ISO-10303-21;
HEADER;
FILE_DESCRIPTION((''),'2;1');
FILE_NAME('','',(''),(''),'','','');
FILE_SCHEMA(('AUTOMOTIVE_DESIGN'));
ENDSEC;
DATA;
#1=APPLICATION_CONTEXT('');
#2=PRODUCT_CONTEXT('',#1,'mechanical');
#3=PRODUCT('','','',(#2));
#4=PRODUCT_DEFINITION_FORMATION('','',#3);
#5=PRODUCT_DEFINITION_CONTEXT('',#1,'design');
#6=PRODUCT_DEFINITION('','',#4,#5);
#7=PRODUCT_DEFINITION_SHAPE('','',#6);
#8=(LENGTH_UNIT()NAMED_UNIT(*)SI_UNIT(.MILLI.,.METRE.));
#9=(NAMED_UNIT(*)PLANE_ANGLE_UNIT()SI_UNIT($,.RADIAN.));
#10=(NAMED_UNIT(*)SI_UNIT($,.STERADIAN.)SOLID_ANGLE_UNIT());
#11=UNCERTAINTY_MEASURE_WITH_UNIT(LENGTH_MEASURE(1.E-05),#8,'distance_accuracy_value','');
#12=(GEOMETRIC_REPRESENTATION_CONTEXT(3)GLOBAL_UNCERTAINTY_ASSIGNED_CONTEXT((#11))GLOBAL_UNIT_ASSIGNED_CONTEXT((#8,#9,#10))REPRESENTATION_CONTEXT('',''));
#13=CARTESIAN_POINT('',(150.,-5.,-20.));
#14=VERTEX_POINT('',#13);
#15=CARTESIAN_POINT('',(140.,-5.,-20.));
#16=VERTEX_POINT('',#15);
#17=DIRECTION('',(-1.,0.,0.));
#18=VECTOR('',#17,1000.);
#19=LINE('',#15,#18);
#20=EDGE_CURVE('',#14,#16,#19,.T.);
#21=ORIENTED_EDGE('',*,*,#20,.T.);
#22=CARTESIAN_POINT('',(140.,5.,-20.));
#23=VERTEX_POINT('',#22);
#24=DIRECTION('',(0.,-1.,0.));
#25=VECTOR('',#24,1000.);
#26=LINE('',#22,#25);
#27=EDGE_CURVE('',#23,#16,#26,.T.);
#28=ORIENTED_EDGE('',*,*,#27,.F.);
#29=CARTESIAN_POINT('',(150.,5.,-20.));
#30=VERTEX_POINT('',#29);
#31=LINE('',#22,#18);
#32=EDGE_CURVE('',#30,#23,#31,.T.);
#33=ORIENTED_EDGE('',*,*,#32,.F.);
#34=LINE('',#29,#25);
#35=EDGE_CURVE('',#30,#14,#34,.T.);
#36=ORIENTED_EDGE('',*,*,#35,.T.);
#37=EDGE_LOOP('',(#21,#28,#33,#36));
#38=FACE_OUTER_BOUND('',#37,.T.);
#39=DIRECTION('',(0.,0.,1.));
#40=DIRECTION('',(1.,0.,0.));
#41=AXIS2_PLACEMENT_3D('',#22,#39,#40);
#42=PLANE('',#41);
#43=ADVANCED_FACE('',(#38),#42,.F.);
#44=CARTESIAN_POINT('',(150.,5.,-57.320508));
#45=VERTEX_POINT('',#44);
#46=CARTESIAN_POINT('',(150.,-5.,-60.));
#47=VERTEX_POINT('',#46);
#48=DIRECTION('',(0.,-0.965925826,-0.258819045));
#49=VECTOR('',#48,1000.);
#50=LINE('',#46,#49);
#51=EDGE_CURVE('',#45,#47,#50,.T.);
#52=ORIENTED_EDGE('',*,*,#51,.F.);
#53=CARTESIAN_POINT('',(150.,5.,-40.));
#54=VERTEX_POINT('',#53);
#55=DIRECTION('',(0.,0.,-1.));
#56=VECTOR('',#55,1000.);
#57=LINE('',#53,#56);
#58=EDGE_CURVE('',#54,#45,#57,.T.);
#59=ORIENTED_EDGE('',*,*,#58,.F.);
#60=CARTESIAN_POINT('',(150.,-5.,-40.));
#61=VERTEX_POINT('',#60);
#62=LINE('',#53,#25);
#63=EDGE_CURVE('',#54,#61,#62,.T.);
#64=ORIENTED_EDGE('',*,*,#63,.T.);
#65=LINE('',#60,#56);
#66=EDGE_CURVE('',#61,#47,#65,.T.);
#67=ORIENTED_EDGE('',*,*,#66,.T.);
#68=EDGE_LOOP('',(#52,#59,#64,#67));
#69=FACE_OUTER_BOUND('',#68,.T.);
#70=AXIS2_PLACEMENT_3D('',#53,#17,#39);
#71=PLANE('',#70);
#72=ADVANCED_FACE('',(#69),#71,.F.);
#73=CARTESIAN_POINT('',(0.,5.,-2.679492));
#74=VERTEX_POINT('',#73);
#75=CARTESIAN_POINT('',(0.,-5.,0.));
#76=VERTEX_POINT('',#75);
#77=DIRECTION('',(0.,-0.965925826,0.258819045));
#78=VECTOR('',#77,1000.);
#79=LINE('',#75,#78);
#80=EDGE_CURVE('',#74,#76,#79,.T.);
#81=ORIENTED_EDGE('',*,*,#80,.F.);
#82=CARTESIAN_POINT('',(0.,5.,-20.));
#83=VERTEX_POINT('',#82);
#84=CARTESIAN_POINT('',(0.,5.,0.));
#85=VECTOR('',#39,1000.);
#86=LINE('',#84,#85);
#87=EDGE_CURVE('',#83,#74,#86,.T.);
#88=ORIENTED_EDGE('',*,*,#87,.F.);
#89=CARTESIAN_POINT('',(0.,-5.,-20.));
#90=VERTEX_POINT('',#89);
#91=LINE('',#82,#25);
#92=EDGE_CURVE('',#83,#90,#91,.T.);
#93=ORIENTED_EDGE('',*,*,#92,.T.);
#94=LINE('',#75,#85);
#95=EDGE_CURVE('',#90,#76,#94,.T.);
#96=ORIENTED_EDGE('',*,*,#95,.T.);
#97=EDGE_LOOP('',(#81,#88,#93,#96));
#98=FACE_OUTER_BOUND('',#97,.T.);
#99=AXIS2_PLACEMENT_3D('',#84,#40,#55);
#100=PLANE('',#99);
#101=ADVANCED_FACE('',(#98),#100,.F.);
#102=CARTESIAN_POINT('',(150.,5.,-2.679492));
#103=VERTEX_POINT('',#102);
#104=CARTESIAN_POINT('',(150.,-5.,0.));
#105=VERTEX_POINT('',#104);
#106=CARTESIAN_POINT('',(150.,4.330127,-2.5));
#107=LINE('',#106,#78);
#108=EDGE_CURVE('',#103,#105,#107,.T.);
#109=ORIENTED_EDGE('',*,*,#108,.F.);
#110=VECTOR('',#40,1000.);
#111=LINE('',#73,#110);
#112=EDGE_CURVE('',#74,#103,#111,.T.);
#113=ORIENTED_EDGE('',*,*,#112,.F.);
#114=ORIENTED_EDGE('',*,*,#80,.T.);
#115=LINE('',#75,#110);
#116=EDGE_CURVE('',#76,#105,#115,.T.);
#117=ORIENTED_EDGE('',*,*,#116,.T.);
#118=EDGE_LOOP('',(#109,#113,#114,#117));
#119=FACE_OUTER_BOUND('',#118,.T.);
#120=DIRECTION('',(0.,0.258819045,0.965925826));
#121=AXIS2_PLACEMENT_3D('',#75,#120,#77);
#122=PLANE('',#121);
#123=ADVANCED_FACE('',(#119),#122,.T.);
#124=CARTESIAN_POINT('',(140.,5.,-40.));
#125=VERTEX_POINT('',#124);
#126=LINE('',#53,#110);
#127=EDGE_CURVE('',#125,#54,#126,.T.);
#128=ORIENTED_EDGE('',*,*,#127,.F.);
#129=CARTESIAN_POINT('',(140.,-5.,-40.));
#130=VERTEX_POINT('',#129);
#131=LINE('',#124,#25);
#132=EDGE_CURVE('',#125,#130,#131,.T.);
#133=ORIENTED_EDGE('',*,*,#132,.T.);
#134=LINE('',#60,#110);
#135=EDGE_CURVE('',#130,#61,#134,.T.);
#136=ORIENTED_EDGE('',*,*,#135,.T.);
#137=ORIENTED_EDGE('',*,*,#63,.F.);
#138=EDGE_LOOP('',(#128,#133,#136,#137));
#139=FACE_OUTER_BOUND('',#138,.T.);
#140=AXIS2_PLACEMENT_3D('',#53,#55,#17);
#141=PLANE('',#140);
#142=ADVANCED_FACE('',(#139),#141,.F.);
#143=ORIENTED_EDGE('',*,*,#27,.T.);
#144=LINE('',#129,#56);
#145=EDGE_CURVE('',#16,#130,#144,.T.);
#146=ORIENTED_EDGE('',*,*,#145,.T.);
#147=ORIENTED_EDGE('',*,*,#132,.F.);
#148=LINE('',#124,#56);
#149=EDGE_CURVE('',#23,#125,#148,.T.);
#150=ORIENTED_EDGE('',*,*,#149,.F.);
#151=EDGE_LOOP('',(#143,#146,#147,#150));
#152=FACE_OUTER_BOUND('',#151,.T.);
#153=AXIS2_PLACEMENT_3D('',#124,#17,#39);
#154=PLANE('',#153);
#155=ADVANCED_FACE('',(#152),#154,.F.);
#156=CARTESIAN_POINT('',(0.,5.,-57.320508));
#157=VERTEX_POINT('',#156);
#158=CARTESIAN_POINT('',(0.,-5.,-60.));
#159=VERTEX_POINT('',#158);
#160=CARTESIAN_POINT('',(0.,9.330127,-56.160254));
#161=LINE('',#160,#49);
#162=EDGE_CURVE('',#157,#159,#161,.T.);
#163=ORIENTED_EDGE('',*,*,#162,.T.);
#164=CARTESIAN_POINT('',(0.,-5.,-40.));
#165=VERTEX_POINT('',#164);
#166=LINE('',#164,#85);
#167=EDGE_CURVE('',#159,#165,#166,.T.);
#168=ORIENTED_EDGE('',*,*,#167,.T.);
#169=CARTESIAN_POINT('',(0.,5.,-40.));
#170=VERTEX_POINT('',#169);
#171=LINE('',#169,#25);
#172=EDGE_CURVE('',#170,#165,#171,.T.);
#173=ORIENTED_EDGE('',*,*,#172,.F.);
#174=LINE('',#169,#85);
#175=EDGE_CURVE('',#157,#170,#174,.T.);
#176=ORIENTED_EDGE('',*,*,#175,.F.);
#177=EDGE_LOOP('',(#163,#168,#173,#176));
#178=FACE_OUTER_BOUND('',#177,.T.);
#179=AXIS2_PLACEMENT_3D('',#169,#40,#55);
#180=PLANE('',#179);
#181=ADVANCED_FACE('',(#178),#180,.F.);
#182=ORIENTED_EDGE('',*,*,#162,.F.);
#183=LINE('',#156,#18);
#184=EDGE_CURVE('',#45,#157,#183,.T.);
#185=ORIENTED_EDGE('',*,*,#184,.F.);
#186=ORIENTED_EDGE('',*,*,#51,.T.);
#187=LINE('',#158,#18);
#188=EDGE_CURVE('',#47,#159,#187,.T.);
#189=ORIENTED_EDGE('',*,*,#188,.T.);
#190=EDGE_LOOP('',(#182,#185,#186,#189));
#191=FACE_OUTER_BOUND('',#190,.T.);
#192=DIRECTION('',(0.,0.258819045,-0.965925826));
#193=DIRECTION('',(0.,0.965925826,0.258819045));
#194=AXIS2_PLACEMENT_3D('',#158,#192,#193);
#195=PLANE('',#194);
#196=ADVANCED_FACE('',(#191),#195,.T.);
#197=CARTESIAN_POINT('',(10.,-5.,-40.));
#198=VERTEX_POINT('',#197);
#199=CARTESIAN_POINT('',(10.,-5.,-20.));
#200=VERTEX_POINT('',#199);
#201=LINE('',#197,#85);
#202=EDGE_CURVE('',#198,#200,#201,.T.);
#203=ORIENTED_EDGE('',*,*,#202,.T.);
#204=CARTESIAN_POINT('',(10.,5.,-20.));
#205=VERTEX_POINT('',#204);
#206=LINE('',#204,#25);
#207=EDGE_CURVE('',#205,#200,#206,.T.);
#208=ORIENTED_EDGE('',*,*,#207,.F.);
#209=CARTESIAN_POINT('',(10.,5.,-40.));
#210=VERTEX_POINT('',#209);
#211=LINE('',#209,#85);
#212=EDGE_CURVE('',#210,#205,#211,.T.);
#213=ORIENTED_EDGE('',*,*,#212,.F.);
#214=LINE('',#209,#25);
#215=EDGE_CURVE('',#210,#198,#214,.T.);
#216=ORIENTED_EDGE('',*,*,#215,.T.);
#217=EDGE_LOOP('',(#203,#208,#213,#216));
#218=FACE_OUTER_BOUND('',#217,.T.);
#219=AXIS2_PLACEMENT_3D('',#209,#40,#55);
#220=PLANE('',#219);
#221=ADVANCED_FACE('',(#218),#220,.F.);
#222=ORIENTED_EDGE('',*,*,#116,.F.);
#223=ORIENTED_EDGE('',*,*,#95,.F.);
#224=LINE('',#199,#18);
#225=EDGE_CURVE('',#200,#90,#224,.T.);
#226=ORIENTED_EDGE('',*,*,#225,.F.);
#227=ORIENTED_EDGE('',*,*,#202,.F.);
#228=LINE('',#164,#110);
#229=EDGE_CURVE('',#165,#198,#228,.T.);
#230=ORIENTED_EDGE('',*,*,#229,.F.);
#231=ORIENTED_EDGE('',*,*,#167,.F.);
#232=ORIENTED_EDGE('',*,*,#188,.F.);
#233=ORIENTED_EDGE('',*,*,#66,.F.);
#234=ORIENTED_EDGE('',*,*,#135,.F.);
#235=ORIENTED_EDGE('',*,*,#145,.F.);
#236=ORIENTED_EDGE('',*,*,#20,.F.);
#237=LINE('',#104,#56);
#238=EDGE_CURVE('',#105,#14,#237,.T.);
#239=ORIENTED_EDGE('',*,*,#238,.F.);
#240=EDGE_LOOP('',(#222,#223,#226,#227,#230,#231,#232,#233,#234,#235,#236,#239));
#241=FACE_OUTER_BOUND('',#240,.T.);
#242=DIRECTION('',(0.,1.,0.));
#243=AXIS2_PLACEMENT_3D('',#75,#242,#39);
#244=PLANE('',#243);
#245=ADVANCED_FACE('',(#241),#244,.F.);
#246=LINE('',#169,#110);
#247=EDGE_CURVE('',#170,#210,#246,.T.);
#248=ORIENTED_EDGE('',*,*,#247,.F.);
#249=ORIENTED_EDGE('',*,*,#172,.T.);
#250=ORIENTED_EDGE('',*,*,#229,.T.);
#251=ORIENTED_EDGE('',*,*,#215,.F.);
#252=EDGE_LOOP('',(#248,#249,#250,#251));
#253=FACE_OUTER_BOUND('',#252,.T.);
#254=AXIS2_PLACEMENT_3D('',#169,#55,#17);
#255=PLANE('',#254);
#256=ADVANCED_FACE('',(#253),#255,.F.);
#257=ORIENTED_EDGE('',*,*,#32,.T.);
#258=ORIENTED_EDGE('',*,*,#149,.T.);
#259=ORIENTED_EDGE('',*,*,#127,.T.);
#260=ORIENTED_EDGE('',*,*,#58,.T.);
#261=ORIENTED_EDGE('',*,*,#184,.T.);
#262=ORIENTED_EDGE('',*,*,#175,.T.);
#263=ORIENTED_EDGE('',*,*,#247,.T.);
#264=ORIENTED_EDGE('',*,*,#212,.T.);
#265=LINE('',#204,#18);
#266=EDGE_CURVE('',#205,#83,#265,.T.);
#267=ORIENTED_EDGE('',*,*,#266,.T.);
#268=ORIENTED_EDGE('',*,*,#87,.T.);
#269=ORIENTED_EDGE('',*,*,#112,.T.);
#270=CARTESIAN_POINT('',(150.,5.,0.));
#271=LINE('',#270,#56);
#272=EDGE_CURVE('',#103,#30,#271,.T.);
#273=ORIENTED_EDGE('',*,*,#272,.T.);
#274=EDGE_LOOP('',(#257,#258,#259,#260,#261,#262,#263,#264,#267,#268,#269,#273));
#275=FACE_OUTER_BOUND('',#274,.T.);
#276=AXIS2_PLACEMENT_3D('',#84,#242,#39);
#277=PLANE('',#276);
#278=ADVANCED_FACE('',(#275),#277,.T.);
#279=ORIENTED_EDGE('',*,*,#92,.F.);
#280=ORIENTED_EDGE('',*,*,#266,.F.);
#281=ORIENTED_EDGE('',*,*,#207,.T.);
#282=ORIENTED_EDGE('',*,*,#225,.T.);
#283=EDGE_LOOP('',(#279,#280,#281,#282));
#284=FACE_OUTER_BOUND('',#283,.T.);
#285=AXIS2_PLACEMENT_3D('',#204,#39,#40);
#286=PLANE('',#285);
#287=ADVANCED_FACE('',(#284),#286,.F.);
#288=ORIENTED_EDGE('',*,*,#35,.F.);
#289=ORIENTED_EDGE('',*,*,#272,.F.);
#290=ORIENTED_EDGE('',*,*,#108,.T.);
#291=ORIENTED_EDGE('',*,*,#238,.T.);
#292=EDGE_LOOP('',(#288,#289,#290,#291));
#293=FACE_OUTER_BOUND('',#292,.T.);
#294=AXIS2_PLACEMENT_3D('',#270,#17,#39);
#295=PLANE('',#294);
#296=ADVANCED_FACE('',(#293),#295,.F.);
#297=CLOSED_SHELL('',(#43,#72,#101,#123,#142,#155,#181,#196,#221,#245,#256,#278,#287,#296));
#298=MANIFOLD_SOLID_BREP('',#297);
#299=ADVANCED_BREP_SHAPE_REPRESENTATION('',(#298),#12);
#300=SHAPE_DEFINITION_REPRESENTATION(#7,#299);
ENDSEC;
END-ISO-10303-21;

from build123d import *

# Parameters (mm, degrees)
TOP_PLATE_150X60X10_DEPTH = 5
FACE_DRAFT_15_A_ANGLE     = -15
FACE_DRAFT_15_B_ANGLE     = -15


with BuildPart() as part:
    # Top Plate Profile → Top Plate 150x60x10 (new, symmetric)
    with BuildSketch(Plane(origin=(0, 0, 0), x_dir=(1, 0, 0), z_dir=(0, 1, 0))):
        Polygon((0, 0), (150, 0), (150, 20), (140, 20), (140, 40), (150, 40), (150, 60), (0, 60), (0, 40), (10, 40), (10, 20), (0, 20), align=None)
    extrude(amount=TOP_PLATE_150X60X10_DEPTH, both=True)

    # Face Draft 15° A
    face_draft_15_a_faces = [part.faces().sort_by_distance(p)[0] for p in [
        (75, 0, 0),
    ]]
    draft(face_draft_15_a_faces, Plane(origin=(0, -5, 0), x_dir=(0, 0, -1), z_dir=(0, -1, 0)), FACE_DRAFT_15_A_ANGLE)

    # Face Draft 15° B
    face_draft_15_b_faces = [part.faces().sort_by_distance(p)[0] for p in [
        (75, 0, -60),
    ]]
    draft(face_draft_15_b_faces, Plane(origin=(0, -5, 0), x_dir=(0, 0, -1), z_dir=(0, -1, 0)), FACE_DRAFT_15_B_ANGLE)


solid = part.part
